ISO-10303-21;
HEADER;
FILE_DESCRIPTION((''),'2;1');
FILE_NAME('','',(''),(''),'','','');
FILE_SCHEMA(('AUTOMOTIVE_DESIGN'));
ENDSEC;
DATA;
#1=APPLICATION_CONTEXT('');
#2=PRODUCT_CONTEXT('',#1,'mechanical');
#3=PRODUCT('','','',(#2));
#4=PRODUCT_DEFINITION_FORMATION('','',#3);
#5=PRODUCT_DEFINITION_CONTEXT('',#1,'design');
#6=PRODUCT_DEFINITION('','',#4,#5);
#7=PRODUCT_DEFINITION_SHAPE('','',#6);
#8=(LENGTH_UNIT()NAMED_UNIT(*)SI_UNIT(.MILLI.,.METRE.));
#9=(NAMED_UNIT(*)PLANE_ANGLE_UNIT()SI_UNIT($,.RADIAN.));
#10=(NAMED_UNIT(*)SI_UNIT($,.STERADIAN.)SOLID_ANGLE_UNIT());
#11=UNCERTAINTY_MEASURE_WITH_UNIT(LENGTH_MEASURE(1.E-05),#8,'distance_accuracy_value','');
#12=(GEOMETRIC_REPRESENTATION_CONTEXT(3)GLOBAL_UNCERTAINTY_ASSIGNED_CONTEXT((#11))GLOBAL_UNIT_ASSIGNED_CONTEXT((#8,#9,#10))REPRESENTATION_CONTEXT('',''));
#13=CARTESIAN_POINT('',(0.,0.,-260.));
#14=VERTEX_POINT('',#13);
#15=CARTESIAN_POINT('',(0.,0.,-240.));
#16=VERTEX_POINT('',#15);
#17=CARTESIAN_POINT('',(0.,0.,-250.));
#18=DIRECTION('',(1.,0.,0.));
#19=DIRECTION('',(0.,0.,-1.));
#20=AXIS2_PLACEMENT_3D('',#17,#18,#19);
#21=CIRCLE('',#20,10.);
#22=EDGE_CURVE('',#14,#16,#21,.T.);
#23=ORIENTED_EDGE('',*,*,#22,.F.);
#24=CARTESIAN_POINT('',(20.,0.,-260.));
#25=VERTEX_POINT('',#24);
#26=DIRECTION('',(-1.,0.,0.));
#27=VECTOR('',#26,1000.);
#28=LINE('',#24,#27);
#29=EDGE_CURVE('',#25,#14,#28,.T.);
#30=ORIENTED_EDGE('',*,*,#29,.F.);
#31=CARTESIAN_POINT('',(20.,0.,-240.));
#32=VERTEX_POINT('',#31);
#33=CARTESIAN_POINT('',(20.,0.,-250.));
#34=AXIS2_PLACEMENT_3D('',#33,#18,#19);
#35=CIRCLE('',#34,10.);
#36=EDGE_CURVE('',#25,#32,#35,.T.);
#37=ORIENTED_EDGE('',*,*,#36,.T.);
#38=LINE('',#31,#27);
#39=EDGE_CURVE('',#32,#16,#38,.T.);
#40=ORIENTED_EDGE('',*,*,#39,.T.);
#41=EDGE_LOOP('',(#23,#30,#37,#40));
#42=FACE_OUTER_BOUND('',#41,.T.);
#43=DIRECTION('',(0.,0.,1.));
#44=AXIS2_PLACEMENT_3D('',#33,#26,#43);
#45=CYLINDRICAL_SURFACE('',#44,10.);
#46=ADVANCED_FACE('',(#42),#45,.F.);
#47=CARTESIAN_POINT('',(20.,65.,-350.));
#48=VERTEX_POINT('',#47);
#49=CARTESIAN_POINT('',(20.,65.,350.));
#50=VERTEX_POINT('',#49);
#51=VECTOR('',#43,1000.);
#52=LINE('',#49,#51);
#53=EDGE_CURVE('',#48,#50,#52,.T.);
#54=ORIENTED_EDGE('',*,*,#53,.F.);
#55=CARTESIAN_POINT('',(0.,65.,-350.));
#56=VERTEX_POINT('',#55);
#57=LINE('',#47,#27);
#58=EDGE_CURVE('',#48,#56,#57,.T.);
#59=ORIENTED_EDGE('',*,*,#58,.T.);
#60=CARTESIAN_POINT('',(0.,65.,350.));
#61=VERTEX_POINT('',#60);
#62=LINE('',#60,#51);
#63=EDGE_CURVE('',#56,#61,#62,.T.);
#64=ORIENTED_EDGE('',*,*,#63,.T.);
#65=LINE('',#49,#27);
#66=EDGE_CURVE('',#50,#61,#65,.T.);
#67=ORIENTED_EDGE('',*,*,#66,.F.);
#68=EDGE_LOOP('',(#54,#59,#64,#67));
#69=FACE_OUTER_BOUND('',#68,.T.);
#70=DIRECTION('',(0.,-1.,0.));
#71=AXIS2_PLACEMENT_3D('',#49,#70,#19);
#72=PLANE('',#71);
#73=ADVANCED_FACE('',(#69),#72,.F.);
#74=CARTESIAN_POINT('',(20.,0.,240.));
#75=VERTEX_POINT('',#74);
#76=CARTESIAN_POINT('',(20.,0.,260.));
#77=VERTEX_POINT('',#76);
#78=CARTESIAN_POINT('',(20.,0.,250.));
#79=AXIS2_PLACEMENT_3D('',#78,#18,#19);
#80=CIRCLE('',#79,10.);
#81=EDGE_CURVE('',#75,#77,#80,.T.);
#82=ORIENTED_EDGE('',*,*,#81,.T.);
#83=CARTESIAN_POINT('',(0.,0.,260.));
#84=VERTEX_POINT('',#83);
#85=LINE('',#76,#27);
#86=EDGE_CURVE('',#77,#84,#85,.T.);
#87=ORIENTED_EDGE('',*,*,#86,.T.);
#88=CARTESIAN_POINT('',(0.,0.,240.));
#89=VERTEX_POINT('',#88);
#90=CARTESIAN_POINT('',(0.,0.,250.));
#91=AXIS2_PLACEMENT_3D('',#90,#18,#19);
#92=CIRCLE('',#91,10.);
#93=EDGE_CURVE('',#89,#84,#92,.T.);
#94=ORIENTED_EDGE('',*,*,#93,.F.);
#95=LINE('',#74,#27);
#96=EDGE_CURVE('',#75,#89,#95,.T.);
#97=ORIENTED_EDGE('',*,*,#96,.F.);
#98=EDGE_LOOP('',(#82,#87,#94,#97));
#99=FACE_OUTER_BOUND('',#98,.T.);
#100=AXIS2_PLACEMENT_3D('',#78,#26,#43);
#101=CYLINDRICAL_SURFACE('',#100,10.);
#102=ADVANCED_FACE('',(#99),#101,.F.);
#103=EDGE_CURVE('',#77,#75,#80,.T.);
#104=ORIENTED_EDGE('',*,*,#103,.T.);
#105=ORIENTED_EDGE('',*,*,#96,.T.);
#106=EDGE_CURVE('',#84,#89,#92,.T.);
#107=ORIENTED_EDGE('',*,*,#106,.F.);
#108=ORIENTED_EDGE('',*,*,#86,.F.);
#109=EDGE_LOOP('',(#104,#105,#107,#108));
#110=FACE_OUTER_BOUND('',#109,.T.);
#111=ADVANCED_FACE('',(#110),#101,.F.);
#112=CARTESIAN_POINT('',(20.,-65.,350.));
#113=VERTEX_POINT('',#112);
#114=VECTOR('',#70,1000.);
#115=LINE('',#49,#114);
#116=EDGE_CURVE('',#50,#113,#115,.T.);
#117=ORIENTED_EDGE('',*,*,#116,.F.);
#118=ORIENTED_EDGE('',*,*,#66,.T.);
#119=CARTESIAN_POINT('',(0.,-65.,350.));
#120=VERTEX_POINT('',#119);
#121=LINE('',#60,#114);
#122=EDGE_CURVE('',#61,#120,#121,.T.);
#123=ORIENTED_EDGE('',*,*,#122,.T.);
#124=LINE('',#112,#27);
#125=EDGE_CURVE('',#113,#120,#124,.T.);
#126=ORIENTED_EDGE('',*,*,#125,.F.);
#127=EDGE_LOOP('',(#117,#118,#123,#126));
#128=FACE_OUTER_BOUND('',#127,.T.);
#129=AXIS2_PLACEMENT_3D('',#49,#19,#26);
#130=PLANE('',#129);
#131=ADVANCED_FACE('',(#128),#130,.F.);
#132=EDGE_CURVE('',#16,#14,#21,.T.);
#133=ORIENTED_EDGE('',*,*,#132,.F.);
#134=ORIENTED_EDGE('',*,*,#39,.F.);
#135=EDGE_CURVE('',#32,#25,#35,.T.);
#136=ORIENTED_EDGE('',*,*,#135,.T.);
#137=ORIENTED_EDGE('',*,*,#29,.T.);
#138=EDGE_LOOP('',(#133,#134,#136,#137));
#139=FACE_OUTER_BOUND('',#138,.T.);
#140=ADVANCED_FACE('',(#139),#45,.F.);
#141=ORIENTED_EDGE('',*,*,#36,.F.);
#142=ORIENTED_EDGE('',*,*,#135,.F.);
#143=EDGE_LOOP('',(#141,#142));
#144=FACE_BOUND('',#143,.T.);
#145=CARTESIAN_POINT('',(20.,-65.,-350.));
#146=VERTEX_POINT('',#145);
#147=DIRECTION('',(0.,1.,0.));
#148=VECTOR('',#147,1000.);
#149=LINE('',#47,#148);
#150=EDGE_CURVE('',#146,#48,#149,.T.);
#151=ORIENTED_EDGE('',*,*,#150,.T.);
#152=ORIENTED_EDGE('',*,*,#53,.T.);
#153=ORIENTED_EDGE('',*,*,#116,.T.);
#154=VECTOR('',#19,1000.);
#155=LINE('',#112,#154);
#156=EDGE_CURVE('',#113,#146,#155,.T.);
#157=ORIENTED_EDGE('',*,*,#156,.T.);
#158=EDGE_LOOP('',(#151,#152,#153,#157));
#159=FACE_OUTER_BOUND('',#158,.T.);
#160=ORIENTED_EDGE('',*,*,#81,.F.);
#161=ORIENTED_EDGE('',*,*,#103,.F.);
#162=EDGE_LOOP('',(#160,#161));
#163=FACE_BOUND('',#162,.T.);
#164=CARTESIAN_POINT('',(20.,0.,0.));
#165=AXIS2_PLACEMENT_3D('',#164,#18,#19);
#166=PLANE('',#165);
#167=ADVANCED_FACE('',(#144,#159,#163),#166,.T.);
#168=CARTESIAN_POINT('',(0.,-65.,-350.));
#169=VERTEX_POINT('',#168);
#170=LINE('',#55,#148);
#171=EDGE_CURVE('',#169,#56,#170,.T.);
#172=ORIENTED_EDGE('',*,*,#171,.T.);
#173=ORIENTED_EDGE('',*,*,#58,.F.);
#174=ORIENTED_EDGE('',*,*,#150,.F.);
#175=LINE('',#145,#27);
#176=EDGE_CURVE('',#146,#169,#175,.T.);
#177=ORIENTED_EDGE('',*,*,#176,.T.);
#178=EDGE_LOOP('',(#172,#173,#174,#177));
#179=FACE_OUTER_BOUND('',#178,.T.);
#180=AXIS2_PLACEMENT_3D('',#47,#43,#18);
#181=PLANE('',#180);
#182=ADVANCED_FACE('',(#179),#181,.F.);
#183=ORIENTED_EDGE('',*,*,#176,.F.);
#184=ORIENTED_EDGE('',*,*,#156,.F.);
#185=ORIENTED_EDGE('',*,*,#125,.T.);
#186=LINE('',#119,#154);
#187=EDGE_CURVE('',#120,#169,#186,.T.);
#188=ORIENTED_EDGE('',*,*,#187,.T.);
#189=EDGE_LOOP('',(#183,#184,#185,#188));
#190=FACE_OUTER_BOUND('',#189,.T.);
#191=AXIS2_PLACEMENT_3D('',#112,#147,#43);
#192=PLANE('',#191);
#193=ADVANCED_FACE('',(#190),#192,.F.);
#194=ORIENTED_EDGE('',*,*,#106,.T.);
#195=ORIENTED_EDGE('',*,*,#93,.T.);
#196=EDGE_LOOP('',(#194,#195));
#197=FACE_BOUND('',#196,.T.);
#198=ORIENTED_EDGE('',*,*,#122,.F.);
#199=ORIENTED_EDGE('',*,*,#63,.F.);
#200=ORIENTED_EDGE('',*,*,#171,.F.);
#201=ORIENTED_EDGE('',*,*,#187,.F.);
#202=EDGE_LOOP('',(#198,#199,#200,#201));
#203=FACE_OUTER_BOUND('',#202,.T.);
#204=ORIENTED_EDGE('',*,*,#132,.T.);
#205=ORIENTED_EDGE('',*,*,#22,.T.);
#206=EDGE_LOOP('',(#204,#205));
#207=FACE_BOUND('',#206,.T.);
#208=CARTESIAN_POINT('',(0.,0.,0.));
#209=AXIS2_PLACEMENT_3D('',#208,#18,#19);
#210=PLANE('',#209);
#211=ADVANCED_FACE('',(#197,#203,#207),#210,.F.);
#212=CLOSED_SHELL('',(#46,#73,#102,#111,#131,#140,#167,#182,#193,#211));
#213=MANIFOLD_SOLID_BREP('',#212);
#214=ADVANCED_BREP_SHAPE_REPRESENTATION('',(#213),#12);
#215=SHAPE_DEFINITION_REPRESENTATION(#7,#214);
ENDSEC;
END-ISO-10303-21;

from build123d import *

# Parameters (mm, degrees)
SKETCH1_W           = 700
SKETCH1_H           = 130
SKETCH1_R           = 10
BOSS_EXTRUDE1_DEPTH = 20


with BuildPart() as part:
    # Sketch1 → Boss-Extrude1 (new body)
    with BuildSketch(Plane(origin=(0, 0, 0), x_dir=(0, 0, -1), z_dir=(1, 0, 0))):
        Rectangle(SKETCH1_W, SKETCH1_H)
        with Locations((-250, 0)):
            Circle(SKETCH1_R, mode=Mode.SUBTRACT)
        with Locations((250, 0)):
            Circle(SKETCH1_R, mode=Mode.SUBTRACT)
    extrude(amount=BOSS_EXTRUDE1_DEPTH)


solid = part.part
